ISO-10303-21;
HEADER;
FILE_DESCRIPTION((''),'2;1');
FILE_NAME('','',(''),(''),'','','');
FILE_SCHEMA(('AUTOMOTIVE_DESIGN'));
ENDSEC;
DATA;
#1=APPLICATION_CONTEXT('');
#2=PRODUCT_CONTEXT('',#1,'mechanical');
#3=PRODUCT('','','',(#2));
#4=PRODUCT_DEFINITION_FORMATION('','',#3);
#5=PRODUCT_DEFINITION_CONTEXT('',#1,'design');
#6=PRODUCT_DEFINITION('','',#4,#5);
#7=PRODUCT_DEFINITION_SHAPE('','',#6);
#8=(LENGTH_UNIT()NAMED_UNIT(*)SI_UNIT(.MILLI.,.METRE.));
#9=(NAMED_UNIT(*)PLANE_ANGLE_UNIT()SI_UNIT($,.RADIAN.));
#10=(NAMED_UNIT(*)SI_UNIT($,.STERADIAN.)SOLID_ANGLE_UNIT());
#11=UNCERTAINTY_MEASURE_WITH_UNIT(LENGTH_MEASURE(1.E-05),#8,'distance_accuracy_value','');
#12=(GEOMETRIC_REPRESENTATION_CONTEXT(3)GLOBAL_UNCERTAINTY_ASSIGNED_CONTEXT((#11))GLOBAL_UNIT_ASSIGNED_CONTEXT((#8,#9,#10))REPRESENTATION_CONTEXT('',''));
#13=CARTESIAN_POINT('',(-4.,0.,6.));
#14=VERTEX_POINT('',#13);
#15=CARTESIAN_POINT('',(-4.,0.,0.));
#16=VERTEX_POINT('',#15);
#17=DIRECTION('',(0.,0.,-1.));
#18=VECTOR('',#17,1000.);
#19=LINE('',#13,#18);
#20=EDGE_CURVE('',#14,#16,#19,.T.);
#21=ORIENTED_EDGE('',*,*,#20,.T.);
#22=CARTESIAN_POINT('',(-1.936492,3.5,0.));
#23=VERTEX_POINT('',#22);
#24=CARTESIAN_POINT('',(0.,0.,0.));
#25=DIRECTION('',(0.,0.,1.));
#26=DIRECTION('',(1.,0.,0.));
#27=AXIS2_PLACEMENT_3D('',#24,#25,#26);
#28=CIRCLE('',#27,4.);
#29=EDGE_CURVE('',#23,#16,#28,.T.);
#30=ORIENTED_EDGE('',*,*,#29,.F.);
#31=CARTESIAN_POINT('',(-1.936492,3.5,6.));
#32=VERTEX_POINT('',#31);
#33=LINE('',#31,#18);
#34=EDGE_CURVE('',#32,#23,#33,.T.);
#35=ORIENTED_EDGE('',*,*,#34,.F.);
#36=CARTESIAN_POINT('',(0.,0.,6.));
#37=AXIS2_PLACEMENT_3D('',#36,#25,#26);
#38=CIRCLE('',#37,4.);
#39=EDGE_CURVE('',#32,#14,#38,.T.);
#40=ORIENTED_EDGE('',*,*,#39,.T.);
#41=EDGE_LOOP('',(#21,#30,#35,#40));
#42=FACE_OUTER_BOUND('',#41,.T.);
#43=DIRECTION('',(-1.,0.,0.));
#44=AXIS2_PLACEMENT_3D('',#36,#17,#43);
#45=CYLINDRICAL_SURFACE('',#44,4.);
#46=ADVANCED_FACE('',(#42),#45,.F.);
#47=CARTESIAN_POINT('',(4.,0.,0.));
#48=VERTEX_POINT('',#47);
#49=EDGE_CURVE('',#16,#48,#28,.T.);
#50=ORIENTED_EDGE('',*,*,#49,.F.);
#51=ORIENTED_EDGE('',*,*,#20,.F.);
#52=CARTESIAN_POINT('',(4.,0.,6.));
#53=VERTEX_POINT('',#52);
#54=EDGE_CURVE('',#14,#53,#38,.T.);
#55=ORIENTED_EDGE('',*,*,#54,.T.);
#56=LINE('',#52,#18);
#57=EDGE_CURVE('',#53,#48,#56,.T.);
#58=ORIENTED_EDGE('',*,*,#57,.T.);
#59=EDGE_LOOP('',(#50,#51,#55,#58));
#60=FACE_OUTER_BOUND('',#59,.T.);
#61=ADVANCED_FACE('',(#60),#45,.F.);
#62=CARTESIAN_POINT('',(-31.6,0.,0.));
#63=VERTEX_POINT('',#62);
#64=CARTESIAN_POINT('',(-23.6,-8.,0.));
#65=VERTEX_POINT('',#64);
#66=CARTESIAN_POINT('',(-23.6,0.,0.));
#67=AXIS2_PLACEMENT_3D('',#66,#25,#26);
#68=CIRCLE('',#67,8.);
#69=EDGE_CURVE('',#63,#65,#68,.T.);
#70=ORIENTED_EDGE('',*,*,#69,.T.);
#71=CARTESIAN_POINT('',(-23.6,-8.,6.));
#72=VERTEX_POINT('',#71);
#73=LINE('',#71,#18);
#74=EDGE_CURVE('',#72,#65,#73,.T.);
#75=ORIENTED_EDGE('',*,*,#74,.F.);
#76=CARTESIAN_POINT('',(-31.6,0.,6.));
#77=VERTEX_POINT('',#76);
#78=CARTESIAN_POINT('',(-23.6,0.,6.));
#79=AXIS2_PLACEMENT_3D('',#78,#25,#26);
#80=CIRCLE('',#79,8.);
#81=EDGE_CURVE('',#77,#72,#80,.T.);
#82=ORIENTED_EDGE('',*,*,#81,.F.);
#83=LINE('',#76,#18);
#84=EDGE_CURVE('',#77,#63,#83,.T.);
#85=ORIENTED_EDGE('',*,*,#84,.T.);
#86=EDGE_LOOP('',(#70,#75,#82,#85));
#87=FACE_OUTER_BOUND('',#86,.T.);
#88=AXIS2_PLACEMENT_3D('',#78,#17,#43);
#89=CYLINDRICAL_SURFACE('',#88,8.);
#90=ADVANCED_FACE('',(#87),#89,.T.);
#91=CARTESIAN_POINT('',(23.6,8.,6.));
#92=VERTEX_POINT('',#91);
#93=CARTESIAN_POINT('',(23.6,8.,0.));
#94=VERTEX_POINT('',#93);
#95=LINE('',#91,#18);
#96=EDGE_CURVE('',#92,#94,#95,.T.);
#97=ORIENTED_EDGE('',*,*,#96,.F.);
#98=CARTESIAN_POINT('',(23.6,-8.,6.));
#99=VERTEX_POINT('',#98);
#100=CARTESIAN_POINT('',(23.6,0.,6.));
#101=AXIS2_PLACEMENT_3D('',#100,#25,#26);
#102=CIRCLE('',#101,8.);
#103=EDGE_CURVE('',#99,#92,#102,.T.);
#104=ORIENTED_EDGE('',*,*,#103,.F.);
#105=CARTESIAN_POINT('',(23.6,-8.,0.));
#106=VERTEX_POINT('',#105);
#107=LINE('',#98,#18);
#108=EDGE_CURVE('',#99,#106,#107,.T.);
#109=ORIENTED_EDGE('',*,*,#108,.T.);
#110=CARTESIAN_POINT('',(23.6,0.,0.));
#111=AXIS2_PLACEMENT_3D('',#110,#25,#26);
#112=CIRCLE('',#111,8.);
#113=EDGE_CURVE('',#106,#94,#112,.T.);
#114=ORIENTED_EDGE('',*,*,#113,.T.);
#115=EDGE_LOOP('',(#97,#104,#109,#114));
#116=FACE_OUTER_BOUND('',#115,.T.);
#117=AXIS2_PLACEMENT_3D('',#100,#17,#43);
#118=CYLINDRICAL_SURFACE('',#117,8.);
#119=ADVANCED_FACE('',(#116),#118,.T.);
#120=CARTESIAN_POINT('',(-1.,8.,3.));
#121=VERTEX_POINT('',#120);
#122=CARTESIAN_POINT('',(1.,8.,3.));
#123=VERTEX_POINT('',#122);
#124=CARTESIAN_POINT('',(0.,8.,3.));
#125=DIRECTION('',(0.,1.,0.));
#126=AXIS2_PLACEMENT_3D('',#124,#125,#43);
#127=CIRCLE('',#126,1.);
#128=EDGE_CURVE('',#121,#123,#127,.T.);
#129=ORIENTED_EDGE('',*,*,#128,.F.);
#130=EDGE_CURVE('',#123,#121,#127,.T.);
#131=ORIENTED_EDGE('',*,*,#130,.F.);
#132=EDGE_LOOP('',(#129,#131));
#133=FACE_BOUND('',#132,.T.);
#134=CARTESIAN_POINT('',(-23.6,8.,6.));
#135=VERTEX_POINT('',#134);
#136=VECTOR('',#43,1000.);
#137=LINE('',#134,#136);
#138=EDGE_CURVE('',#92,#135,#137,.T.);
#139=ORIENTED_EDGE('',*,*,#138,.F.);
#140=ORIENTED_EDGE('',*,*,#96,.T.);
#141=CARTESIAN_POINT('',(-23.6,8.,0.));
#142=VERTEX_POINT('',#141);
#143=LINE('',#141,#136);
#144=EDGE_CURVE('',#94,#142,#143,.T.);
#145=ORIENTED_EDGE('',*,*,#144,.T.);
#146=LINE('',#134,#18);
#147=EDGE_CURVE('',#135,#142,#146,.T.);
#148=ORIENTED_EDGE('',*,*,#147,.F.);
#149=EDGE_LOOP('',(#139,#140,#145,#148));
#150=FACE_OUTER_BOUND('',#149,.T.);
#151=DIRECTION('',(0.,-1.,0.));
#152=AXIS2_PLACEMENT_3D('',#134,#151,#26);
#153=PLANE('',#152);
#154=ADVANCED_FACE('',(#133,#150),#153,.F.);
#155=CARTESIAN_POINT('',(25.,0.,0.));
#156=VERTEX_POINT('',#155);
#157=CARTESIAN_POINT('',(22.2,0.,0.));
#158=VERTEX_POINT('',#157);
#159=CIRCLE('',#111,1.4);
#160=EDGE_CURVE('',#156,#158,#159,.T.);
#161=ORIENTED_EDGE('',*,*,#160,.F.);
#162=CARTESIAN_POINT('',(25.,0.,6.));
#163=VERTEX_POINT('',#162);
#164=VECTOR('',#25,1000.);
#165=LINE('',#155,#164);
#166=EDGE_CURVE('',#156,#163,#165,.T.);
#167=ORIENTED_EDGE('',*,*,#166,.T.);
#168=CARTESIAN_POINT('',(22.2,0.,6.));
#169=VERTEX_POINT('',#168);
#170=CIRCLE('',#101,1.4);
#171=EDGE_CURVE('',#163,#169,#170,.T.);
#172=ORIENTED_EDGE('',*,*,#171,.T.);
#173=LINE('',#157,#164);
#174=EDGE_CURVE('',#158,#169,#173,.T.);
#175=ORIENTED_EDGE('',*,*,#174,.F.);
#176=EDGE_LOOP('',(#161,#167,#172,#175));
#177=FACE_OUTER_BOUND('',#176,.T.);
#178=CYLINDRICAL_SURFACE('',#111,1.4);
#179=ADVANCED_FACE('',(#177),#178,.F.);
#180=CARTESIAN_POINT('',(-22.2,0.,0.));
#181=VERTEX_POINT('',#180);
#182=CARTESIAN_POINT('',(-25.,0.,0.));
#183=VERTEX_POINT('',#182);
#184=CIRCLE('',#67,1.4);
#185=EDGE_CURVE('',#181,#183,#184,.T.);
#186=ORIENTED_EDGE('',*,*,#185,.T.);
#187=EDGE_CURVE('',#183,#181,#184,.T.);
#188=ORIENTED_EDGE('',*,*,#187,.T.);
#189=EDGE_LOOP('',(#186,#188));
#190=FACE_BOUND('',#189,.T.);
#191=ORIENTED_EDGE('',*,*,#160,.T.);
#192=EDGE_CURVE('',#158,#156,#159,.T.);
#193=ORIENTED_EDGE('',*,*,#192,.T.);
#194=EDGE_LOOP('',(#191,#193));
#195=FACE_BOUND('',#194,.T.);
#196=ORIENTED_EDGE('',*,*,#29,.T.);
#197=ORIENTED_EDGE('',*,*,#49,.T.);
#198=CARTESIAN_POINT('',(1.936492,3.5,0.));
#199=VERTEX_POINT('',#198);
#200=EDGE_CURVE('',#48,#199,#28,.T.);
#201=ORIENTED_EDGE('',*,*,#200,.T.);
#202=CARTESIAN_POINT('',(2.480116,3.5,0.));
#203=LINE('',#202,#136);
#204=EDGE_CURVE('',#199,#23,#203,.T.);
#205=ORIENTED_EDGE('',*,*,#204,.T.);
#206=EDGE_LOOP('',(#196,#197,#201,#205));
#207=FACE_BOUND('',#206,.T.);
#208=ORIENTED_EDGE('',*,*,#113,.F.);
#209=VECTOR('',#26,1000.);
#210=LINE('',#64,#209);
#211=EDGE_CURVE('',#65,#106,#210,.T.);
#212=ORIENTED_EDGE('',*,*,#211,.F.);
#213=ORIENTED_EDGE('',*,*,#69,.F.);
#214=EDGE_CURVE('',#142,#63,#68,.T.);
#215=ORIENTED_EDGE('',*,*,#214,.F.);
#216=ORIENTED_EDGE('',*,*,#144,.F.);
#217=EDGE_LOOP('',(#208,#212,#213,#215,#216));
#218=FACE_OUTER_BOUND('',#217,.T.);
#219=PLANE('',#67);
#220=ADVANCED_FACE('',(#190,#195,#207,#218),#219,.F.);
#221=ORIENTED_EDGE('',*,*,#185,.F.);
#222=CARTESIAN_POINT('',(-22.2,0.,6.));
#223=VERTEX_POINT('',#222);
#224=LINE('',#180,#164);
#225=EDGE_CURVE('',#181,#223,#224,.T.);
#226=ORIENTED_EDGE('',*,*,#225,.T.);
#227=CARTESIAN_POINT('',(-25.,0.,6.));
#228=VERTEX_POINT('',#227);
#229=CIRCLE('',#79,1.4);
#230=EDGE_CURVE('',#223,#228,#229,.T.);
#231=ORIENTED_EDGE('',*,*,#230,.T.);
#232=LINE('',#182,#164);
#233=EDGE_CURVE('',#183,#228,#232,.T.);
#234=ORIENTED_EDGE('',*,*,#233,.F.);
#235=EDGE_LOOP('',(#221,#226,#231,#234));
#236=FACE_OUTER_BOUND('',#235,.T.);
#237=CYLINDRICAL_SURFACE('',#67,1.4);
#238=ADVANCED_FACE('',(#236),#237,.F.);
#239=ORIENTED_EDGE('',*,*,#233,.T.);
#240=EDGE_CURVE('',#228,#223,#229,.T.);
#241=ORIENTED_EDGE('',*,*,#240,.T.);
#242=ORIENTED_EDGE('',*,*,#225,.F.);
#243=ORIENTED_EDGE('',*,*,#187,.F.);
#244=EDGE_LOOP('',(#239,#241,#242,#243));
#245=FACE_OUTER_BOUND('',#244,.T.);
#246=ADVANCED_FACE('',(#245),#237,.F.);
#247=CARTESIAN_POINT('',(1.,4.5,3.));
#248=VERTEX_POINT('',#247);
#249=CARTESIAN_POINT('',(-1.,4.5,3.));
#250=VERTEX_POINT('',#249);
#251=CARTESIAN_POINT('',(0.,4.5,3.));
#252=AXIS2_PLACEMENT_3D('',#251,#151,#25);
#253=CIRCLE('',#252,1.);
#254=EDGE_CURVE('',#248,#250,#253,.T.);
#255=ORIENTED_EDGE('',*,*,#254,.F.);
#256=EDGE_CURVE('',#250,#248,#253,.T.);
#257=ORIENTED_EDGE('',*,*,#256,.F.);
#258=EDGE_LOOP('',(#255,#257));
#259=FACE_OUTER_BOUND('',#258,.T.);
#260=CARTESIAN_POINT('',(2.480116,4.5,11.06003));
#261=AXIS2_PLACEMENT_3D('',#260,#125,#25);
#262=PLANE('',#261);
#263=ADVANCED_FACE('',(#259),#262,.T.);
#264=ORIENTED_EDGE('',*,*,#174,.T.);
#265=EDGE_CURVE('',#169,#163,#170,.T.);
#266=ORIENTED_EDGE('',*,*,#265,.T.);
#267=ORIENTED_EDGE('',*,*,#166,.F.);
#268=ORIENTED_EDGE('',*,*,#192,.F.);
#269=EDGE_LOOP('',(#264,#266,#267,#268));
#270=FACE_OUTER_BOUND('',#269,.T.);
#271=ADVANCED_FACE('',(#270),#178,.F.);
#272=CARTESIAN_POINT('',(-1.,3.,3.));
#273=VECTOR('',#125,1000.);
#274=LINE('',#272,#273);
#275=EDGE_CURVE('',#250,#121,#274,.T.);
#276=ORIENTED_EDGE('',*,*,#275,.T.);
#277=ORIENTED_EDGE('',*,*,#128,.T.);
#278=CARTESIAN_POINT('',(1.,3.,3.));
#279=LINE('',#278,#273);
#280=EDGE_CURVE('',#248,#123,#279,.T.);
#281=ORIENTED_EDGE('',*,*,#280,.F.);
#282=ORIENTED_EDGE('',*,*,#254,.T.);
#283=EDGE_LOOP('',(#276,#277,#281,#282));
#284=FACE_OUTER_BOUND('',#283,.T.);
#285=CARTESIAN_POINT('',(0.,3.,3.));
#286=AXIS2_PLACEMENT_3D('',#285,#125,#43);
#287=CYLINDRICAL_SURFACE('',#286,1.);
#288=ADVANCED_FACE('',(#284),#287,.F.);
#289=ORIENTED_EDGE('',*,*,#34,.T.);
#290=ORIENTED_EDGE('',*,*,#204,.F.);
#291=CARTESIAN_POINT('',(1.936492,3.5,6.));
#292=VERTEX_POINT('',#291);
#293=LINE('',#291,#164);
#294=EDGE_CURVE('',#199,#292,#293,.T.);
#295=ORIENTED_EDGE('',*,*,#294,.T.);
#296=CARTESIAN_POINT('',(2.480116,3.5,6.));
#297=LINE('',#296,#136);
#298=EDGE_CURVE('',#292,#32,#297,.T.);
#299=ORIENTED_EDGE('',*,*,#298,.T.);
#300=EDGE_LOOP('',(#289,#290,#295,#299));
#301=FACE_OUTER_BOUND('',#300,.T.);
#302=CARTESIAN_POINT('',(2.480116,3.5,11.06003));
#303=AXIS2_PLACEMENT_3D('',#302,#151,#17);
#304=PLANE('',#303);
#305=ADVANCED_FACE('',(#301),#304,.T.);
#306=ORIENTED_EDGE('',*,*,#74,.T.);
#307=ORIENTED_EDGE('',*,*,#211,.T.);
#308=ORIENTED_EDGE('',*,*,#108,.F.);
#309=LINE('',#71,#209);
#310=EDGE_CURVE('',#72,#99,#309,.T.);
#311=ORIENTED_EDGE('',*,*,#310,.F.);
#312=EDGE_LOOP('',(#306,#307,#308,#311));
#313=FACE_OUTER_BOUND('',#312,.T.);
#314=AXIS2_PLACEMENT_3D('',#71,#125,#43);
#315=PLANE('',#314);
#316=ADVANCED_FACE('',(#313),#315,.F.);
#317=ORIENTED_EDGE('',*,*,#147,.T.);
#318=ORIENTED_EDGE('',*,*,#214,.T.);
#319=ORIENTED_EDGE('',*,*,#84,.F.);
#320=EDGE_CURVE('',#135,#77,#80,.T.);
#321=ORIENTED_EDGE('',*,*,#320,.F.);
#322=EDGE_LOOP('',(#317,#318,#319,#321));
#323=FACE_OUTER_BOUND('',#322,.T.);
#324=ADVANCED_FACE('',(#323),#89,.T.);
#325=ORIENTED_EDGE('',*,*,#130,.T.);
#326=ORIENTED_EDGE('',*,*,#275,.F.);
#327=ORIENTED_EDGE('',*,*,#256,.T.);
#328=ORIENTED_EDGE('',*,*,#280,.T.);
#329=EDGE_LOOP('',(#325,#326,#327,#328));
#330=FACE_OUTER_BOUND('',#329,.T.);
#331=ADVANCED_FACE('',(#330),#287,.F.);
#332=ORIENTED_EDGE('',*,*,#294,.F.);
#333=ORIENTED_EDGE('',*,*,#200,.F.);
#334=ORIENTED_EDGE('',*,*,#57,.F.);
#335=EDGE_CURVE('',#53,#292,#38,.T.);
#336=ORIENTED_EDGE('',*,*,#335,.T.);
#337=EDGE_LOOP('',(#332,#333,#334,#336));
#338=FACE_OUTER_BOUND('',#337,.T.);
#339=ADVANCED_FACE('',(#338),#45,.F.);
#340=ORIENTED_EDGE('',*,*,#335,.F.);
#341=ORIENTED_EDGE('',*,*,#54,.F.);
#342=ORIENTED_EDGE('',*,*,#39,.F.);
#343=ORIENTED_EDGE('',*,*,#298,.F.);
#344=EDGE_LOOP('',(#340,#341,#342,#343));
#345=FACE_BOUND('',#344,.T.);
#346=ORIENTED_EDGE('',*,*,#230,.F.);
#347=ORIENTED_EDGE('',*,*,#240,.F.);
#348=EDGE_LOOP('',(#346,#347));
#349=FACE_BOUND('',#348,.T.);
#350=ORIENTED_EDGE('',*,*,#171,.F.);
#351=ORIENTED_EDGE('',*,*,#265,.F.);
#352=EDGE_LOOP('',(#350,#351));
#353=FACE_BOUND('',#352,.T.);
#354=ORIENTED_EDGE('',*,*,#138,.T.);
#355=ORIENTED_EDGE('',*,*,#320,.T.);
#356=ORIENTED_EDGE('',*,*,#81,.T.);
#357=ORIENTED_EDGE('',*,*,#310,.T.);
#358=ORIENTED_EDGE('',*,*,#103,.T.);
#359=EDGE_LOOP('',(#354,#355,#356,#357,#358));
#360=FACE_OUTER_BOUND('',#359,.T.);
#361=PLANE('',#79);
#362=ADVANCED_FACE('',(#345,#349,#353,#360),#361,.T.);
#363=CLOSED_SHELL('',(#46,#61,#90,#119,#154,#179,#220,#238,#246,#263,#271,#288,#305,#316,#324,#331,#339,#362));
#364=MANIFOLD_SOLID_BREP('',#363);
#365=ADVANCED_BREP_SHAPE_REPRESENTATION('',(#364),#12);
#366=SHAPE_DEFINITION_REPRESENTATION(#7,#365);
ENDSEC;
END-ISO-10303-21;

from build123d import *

# Parameters (mm, degrees)
SKETCH_1_R          = 4
EXTRUDE_1_DEPTH     = 6
SKETCH_2_R          = 1.4
CUT_EXTRUDE_1_DEPTH = 34.144531977
SKETCH_3_R          = 1
CUT_EXTRUDE_2_DEPTH = 5
SKETCH_4_W          = 4.960231778
SKETCH_4_H          = 1
EXTRUDE_2_DEPTH     = 6


with BuildPart() as part:
    # 草图1 → 凸台-拉伸1 (new body)
    with BuildSketch(Plane.XY):
        with BuildLine():
            Line((-23.6, 8), (23.6, 8))
            ThreePointArc((23.6, 8), (31.6, 0), (23.6, -8))
            Line((23.6, -8), (-23.6, -8))
            ThreePointArc((-23.6, -8), (-31.6, 0), (-23.6, 8))
        make_face()
        Circle(SKETCH_1_R, mode=Mode.SUBTRACT)
    extrude(amount=EXTRUDE_1_DEPTH)

    # 草图2 → 切除-拉伸1 (cut, through all)
    with BuildSketch(Plane.XY.offset(6)):
        with Locations((-23.6, 0)):
            Circle(SKETCH_2_R)
        with Locations((23.6, 0)):
            Circle(SKETCH_2_R)
    extrude(amount=-CUT_EXTRUDE_1_DEPTH, mode=Mode.SUBTRACT)

    # 草图3 → 切除-拉伸2 (cut)
    with BuildSketch(Plane(origin=(0, 8, 0), x_dir=(1, 0, 0), z_dir=(0, 1, 0))):
        with Locations(Location((0, -3, 0), (0, 0, 180))):
            Circle(SKETCH_3_R)
    extrude(amount=-CUT_EXTRUDE_2_DEPTH, mode=Mode.SUBTRACT)

    # 草图4 → 凸台-拉伸2 (add)
    with BuildSketch(Plane(origin=(0, 0, 0), x_dir=(-1, 0, 0), z_dir=(0, 0, -1))):
        with Locations((0, 4)):
            Rectangle(SKETCH_4_W, SKETCH_4_H)
    extrude(amount=-EXTRUDE_2_DEPTH)


solid = part.part
